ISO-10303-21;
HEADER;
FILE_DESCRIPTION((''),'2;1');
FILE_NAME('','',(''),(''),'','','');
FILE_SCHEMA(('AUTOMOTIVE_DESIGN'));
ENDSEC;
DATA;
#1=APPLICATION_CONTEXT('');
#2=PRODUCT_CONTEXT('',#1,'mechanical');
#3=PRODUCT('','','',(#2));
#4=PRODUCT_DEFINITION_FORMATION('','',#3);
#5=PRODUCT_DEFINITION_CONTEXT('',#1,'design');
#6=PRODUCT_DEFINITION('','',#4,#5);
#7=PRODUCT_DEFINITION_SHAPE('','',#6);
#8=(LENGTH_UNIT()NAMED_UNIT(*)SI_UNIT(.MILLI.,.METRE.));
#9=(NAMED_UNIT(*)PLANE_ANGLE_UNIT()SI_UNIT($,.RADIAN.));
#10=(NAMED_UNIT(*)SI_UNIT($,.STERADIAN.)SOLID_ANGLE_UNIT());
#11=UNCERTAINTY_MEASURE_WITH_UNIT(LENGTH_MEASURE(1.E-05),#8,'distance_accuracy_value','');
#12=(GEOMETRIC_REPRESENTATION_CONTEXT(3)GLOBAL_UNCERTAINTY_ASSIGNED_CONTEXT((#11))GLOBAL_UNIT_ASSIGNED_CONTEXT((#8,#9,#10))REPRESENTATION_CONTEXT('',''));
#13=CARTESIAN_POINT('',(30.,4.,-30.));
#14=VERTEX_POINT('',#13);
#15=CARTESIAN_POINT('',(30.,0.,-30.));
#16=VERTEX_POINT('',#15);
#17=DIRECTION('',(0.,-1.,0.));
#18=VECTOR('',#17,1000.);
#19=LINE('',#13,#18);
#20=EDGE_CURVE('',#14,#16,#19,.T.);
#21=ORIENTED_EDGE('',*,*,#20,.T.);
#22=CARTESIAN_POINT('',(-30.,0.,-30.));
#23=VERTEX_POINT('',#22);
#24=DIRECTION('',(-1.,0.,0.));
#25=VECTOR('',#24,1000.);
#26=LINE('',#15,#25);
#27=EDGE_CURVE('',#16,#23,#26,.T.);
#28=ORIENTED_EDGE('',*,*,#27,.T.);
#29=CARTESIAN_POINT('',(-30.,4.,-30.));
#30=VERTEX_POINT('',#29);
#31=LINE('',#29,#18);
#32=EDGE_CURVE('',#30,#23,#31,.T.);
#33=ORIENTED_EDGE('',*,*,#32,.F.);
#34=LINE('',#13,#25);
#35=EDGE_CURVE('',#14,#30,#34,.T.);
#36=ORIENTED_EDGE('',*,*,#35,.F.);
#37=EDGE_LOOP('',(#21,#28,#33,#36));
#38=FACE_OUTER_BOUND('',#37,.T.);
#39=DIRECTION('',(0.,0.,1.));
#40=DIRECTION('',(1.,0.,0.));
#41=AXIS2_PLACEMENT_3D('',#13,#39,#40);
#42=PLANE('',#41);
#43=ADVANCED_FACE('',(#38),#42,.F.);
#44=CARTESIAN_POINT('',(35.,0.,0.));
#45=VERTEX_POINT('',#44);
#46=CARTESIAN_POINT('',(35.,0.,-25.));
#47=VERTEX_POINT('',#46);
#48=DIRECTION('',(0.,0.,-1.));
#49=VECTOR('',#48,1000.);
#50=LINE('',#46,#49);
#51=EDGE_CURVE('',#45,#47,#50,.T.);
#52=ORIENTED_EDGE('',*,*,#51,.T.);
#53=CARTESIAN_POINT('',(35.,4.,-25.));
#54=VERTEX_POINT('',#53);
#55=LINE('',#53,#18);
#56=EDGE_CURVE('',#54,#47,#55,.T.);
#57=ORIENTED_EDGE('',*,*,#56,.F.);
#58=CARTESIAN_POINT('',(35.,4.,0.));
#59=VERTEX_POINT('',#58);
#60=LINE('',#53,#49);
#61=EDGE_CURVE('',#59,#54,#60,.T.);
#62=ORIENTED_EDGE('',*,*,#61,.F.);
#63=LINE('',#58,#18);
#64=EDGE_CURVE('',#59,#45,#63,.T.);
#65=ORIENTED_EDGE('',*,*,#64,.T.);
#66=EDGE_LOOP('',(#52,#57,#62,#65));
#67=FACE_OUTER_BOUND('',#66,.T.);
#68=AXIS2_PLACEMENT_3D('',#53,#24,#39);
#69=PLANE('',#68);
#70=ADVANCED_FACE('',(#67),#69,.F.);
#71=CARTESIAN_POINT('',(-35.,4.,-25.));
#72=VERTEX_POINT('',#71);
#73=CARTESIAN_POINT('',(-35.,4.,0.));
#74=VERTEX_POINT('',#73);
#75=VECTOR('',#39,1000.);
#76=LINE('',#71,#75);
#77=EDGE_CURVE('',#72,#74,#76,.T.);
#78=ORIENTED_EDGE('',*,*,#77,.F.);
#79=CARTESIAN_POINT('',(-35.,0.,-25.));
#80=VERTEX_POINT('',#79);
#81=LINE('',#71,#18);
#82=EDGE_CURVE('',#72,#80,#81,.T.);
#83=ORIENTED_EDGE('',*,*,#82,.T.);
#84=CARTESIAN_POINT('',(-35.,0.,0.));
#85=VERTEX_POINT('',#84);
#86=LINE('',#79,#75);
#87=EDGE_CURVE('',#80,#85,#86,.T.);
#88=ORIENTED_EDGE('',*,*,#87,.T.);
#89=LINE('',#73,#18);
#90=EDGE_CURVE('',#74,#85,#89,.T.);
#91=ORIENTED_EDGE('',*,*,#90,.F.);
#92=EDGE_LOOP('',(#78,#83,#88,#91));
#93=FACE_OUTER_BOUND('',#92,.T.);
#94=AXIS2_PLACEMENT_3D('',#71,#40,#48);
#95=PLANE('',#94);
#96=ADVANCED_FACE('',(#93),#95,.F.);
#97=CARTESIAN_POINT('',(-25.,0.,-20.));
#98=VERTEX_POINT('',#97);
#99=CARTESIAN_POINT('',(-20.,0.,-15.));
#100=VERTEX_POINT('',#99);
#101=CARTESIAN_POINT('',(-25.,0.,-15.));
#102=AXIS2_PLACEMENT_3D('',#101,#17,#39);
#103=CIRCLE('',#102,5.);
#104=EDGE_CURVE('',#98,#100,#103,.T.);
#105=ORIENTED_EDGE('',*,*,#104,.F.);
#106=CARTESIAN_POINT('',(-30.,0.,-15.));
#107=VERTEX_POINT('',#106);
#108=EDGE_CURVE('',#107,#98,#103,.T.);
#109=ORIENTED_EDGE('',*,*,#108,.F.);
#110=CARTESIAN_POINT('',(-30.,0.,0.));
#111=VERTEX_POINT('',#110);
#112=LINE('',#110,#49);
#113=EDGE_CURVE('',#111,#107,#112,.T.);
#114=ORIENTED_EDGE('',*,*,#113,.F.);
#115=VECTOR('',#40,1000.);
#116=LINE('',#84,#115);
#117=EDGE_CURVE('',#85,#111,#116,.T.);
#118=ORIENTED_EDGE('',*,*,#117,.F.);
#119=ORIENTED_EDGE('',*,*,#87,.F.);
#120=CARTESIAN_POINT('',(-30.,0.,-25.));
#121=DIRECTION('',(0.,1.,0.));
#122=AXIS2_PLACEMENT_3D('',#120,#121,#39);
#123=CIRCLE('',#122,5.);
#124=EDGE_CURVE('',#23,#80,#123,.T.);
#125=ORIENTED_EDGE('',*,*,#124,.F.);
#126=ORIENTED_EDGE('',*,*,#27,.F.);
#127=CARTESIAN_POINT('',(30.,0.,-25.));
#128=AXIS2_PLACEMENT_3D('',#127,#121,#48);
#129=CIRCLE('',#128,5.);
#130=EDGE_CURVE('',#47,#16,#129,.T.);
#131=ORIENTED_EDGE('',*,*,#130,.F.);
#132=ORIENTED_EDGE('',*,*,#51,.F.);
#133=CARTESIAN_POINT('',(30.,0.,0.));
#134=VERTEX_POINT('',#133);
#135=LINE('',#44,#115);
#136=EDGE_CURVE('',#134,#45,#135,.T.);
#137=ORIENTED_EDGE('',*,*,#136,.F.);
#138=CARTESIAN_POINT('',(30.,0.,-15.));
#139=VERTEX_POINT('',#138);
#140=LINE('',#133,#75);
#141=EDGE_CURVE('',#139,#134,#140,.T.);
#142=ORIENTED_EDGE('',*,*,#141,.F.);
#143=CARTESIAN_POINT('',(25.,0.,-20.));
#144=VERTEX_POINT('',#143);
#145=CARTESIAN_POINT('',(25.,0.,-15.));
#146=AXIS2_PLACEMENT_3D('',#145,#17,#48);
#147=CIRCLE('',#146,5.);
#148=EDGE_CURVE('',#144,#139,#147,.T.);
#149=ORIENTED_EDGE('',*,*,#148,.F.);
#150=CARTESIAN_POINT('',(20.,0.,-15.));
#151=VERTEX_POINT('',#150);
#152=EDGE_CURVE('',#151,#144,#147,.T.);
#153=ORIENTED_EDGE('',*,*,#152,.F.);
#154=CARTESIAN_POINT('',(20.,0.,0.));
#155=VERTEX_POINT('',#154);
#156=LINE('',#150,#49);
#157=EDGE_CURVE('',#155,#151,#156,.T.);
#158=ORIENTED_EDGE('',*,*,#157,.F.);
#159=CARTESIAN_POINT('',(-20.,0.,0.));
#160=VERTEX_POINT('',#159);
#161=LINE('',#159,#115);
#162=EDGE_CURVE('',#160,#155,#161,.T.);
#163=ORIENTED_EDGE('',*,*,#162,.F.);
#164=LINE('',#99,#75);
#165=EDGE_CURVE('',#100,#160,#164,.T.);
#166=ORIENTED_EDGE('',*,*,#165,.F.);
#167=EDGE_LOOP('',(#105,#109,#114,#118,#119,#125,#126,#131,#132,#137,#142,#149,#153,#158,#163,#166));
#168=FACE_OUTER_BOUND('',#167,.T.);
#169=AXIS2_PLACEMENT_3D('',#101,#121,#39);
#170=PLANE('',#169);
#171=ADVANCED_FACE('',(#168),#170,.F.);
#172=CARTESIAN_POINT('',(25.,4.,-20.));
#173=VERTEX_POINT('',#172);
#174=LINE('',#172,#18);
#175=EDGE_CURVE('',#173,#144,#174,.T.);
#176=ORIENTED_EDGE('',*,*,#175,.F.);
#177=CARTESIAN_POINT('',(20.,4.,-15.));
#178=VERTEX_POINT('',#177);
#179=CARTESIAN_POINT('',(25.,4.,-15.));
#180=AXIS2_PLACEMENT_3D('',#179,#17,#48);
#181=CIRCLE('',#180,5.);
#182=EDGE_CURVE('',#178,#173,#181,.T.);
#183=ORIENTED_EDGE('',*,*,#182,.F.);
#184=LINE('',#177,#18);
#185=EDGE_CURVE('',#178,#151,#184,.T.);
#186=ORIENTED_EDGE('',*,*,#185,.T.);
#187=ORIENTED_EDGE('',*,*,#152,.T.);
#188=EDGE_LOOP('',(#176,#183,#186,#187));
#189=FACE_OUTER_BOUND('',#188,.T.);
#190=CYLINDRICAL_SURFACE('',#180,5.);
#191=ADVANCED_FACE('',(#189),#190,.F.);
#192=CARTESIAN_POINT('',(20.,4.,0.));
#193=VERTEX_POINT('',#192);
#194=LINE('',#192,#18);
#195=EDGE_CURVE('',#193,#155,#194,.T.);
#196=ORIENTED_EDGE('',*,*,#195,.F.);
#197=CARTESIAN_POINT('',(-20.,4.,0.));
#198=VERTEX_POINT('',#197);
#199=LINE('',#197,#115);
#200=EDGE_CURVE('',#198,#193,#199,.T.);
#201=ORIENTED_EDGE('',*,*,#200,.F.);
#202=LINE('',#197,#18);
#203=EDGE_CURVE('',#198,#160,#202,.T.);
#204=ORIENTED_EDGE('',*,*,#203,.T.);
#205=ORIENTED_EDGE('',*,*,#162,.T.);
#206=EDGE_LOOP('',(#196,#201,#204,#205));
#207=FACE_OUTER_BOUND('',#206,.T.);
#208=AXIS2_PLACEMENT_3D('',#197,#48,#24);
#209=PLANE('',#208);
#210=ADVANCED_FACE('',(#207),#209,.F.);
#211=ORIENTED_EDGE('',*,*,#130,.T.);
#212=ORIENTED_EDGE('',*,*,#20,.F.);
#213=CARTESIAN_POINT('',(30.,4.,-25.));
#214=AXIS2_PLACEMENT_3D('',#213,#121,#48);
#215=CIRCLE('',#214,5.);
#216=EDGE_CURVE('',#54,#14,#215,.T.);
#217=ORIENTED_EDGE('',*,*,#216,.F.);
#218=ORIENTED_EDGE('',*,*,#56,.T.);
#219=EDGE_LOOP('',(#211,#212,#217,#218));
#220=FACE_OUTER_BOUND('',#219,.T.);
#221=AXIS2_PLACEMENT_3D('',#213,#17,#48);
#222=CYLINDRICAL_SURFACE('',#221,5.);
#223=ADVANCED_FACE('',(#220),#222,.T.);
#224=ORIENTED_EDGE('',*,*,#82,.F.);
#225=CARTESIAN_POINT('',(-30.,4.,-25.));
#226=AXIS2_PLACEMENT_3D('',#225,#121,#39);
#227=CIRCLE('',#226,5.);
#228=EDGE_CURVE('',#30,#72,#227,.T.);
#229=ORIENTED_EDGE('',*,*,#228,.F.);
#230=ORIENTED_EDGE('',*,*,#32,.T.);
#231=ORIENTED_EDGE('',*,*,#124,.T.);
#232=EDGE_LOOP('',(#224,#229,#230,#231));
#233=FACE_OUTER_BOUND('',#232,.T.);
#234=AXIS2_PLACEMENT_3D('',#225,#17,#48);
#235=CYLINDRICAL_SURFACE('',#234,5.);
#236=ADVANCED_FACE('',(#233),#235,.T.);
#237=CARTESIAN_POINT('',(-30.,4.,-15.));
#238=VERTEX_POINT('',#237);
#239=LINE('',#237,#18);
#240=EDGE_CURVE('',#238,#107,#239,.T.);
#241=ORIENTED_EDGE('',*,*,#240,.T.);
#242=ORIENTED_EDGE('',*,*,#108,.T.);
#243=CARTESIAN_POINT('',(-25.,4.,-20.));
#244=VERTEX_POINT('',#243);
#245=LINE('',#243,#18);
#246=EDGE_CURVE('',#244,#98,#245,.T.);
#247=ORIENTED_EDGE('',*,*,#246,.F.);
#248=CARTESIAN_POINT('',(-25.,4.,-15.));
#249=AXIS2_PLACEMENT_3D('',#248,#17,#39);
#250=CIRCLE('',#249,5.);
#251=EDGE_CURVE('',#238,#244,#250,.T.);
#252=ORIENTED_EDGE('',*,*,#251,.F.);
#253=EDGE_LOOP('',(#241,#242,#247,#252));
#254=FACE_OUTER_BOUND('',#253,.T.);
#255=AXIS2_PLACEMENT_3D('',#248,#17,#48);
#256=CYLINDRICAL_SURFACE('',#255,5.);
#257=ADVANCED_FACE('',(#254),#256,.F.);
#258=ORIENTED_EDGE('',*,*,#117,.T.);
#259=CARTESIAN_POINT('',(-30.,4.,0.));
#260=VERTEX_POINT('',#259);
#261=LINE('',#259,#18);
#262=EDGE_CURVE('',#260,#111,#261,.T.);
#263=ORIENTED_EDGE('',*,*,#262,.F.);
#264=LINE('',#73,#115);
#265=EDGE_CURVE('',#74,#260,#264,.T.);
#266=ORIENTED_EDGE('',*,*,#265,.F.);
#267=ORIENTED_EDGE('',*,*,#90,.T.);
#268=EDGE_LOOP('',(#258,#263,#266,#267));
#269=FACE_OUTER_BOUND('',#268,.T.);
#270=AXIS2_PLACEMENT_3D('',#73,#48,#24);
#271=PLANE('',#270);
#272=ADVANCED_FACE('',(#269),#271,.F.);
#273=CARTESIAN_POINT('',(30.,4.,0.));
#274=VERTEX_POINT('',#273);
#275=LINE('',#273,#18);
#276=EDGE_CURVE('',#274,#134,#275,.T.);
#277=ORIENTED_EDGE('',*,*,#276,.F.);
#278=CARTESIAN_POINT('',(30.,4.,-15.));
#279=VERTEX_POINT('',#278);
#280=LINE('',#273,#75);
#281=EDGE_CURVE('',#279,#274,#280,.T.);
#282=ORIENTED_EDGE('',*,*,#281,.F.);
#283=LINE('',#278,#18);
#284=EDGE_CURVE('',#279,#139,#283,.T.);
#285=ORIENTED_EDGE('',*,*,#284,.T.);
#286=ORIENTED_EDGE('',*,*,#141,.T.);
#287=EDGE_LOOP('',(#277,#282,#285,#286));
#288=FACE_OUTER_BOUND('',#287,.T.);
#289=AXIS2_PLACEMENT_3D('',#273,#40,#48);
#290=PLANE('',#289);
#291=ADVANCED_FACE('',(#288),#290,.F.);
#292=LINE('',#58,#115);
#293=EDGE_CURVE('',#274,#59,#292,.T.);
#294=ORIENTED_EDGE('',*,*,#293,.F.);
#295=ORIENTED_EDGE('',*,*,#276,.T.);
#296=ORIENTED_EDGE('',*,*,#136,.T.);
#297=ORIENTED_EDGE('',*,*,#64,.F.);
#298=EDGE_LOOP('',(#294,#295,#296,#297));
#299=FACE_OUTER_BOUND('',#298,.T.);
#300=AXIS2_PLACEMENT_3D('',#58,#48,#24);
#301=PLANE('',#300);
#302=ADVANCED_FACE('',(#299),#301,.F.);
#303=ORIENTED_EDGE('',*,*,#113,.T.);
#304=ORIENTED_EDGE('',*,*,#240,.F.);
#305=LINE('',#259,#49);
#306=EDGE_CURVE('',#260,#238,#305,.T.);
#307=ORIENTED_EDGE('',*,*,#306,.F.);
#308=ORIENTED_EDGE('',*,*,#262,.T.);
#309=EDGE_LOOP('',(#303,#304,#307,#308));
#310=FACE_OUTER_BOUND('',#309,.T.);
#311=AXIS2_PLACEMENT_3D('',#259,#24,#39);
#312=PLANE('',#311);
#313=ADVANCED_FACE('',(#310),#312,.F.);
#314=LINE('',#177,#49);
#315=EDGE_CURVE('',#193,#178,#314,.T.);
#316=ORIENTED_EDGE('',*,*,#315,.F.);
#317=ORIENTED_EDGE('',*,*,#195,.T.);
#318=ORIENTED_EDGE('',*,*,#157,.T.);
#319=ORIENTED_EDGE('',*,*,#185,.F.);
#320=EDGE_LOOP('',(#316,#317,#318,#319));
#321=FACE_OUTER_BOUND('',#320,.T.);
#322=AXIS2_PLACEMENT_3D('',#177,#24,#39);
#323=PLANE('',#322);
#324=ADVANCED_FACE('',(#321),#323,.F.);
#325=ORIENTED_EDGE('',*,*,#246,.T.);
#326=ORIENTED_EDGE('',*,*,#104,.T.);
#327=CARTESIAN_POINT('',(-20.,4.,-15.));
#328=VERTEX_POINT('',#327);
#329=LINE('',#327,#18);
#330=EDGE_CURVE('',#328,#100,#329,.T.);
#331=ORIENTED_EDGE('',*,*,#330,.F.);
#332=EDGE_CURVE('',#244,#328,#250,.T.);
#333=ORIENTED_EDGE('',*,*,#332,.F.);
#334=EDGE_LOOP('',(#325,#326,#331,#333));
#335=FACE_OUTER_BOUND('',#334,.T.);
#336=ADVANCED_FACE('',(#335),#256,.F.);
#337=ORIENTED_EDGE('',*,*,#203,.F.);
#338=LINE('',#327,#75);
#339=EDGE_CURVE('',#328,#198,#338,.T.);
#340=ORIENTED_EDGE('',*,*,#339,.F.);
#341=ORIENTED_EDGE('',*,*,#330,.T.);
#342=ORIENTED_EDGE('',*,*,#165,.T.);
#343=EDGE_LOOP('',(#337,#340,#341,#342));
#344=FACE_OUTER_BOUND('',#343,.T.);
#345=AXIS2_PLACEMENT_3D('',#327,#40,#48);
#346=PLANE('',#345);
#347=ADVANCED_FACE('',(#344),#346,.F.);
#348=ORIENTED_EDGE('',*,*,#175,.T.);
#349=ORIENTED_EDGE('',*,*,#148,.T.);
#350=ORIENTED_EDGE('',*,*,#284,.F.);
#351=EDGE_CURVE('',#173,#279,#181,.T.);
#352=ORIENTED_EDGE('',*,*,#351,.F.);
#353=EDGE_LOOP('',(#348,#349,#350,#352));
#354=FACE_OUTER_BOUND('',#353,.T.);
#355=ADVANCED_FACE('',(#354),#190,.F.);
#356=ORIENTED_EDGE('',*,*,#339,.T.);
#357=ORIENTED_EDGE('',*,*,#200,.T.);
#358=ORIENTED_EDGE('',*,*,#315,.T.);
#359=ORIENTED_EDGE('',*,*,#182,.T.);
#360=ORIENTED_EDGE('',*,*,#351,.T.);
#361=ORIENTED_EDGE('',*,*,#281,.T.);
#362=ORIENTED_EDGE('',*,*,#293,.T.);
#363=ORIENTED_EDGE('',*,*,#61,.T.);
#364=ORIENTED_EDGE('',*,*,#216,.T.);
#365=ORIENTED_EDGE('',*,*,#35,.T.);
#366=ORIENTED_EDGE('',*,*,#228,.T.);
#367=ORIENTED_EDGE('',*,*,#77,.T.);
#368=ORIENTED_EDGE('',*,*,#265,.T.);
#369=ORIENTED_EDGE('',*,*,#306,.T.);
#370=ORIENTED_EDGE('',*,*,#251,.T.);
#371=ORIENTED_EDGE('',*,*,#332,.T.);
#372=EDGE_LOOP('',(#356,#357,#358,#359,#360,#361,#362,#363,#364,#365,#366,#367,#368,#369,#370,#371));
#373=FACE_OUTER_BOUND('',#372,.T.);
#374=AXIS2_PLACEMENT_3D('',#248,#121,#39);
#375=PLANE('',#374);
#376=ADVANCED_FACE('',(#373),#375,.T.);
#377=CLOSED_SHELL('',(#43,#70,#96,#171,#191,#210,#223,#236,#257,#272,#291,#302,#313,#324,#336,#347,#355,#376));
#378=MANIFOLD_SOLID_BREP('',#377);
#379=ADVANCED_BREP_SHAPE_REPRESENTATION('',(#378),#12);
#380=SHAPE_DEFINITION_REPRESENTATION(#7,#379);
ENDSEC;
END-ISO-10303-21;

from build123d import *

# Parameters (mm, degrees)
EXTRUDE_1_DEPTH = 4


with BuildPart() as part:
    # 草图1 → 凸台-拉伸1 (new body)
    with BuildSketch(Plane(origin=(0, 0, 0), x_dir=(1, 0, 0), z_dir=(0, 1, 0))):
        with BuildLine():
            Line((30, 30), (-30, 30))
            ThreePointArc((-30, 30), (-33.535533906, 28.535533906), (-35, 25))
            Line((-35, 25), (-35, 0))
            Line((-35, 0), (-30, 0))
            Line((-30, 0), (-30, 15))
            ThreePointArc((-30, 15), (-25, 20), (-20, 15))
            Line((-20, 15), (-20, 0))
            Line((-20, 0), (20, 0))
            Line((20, 0), (20, 15))
            ThreePointArc((20, 15), (25, 20), (30, 15))
            Line((30, 15), (30, 0))
            Line((30, 0), (35, 0))
            Line((35, 0), (35, 25))
            ThreePointArc((35, 25), (33.535533906, 28.535533906), (30, 30))
        make_face()
    extrude(amount=EXTRUDE_1_DEPTH)


solid = part.part
